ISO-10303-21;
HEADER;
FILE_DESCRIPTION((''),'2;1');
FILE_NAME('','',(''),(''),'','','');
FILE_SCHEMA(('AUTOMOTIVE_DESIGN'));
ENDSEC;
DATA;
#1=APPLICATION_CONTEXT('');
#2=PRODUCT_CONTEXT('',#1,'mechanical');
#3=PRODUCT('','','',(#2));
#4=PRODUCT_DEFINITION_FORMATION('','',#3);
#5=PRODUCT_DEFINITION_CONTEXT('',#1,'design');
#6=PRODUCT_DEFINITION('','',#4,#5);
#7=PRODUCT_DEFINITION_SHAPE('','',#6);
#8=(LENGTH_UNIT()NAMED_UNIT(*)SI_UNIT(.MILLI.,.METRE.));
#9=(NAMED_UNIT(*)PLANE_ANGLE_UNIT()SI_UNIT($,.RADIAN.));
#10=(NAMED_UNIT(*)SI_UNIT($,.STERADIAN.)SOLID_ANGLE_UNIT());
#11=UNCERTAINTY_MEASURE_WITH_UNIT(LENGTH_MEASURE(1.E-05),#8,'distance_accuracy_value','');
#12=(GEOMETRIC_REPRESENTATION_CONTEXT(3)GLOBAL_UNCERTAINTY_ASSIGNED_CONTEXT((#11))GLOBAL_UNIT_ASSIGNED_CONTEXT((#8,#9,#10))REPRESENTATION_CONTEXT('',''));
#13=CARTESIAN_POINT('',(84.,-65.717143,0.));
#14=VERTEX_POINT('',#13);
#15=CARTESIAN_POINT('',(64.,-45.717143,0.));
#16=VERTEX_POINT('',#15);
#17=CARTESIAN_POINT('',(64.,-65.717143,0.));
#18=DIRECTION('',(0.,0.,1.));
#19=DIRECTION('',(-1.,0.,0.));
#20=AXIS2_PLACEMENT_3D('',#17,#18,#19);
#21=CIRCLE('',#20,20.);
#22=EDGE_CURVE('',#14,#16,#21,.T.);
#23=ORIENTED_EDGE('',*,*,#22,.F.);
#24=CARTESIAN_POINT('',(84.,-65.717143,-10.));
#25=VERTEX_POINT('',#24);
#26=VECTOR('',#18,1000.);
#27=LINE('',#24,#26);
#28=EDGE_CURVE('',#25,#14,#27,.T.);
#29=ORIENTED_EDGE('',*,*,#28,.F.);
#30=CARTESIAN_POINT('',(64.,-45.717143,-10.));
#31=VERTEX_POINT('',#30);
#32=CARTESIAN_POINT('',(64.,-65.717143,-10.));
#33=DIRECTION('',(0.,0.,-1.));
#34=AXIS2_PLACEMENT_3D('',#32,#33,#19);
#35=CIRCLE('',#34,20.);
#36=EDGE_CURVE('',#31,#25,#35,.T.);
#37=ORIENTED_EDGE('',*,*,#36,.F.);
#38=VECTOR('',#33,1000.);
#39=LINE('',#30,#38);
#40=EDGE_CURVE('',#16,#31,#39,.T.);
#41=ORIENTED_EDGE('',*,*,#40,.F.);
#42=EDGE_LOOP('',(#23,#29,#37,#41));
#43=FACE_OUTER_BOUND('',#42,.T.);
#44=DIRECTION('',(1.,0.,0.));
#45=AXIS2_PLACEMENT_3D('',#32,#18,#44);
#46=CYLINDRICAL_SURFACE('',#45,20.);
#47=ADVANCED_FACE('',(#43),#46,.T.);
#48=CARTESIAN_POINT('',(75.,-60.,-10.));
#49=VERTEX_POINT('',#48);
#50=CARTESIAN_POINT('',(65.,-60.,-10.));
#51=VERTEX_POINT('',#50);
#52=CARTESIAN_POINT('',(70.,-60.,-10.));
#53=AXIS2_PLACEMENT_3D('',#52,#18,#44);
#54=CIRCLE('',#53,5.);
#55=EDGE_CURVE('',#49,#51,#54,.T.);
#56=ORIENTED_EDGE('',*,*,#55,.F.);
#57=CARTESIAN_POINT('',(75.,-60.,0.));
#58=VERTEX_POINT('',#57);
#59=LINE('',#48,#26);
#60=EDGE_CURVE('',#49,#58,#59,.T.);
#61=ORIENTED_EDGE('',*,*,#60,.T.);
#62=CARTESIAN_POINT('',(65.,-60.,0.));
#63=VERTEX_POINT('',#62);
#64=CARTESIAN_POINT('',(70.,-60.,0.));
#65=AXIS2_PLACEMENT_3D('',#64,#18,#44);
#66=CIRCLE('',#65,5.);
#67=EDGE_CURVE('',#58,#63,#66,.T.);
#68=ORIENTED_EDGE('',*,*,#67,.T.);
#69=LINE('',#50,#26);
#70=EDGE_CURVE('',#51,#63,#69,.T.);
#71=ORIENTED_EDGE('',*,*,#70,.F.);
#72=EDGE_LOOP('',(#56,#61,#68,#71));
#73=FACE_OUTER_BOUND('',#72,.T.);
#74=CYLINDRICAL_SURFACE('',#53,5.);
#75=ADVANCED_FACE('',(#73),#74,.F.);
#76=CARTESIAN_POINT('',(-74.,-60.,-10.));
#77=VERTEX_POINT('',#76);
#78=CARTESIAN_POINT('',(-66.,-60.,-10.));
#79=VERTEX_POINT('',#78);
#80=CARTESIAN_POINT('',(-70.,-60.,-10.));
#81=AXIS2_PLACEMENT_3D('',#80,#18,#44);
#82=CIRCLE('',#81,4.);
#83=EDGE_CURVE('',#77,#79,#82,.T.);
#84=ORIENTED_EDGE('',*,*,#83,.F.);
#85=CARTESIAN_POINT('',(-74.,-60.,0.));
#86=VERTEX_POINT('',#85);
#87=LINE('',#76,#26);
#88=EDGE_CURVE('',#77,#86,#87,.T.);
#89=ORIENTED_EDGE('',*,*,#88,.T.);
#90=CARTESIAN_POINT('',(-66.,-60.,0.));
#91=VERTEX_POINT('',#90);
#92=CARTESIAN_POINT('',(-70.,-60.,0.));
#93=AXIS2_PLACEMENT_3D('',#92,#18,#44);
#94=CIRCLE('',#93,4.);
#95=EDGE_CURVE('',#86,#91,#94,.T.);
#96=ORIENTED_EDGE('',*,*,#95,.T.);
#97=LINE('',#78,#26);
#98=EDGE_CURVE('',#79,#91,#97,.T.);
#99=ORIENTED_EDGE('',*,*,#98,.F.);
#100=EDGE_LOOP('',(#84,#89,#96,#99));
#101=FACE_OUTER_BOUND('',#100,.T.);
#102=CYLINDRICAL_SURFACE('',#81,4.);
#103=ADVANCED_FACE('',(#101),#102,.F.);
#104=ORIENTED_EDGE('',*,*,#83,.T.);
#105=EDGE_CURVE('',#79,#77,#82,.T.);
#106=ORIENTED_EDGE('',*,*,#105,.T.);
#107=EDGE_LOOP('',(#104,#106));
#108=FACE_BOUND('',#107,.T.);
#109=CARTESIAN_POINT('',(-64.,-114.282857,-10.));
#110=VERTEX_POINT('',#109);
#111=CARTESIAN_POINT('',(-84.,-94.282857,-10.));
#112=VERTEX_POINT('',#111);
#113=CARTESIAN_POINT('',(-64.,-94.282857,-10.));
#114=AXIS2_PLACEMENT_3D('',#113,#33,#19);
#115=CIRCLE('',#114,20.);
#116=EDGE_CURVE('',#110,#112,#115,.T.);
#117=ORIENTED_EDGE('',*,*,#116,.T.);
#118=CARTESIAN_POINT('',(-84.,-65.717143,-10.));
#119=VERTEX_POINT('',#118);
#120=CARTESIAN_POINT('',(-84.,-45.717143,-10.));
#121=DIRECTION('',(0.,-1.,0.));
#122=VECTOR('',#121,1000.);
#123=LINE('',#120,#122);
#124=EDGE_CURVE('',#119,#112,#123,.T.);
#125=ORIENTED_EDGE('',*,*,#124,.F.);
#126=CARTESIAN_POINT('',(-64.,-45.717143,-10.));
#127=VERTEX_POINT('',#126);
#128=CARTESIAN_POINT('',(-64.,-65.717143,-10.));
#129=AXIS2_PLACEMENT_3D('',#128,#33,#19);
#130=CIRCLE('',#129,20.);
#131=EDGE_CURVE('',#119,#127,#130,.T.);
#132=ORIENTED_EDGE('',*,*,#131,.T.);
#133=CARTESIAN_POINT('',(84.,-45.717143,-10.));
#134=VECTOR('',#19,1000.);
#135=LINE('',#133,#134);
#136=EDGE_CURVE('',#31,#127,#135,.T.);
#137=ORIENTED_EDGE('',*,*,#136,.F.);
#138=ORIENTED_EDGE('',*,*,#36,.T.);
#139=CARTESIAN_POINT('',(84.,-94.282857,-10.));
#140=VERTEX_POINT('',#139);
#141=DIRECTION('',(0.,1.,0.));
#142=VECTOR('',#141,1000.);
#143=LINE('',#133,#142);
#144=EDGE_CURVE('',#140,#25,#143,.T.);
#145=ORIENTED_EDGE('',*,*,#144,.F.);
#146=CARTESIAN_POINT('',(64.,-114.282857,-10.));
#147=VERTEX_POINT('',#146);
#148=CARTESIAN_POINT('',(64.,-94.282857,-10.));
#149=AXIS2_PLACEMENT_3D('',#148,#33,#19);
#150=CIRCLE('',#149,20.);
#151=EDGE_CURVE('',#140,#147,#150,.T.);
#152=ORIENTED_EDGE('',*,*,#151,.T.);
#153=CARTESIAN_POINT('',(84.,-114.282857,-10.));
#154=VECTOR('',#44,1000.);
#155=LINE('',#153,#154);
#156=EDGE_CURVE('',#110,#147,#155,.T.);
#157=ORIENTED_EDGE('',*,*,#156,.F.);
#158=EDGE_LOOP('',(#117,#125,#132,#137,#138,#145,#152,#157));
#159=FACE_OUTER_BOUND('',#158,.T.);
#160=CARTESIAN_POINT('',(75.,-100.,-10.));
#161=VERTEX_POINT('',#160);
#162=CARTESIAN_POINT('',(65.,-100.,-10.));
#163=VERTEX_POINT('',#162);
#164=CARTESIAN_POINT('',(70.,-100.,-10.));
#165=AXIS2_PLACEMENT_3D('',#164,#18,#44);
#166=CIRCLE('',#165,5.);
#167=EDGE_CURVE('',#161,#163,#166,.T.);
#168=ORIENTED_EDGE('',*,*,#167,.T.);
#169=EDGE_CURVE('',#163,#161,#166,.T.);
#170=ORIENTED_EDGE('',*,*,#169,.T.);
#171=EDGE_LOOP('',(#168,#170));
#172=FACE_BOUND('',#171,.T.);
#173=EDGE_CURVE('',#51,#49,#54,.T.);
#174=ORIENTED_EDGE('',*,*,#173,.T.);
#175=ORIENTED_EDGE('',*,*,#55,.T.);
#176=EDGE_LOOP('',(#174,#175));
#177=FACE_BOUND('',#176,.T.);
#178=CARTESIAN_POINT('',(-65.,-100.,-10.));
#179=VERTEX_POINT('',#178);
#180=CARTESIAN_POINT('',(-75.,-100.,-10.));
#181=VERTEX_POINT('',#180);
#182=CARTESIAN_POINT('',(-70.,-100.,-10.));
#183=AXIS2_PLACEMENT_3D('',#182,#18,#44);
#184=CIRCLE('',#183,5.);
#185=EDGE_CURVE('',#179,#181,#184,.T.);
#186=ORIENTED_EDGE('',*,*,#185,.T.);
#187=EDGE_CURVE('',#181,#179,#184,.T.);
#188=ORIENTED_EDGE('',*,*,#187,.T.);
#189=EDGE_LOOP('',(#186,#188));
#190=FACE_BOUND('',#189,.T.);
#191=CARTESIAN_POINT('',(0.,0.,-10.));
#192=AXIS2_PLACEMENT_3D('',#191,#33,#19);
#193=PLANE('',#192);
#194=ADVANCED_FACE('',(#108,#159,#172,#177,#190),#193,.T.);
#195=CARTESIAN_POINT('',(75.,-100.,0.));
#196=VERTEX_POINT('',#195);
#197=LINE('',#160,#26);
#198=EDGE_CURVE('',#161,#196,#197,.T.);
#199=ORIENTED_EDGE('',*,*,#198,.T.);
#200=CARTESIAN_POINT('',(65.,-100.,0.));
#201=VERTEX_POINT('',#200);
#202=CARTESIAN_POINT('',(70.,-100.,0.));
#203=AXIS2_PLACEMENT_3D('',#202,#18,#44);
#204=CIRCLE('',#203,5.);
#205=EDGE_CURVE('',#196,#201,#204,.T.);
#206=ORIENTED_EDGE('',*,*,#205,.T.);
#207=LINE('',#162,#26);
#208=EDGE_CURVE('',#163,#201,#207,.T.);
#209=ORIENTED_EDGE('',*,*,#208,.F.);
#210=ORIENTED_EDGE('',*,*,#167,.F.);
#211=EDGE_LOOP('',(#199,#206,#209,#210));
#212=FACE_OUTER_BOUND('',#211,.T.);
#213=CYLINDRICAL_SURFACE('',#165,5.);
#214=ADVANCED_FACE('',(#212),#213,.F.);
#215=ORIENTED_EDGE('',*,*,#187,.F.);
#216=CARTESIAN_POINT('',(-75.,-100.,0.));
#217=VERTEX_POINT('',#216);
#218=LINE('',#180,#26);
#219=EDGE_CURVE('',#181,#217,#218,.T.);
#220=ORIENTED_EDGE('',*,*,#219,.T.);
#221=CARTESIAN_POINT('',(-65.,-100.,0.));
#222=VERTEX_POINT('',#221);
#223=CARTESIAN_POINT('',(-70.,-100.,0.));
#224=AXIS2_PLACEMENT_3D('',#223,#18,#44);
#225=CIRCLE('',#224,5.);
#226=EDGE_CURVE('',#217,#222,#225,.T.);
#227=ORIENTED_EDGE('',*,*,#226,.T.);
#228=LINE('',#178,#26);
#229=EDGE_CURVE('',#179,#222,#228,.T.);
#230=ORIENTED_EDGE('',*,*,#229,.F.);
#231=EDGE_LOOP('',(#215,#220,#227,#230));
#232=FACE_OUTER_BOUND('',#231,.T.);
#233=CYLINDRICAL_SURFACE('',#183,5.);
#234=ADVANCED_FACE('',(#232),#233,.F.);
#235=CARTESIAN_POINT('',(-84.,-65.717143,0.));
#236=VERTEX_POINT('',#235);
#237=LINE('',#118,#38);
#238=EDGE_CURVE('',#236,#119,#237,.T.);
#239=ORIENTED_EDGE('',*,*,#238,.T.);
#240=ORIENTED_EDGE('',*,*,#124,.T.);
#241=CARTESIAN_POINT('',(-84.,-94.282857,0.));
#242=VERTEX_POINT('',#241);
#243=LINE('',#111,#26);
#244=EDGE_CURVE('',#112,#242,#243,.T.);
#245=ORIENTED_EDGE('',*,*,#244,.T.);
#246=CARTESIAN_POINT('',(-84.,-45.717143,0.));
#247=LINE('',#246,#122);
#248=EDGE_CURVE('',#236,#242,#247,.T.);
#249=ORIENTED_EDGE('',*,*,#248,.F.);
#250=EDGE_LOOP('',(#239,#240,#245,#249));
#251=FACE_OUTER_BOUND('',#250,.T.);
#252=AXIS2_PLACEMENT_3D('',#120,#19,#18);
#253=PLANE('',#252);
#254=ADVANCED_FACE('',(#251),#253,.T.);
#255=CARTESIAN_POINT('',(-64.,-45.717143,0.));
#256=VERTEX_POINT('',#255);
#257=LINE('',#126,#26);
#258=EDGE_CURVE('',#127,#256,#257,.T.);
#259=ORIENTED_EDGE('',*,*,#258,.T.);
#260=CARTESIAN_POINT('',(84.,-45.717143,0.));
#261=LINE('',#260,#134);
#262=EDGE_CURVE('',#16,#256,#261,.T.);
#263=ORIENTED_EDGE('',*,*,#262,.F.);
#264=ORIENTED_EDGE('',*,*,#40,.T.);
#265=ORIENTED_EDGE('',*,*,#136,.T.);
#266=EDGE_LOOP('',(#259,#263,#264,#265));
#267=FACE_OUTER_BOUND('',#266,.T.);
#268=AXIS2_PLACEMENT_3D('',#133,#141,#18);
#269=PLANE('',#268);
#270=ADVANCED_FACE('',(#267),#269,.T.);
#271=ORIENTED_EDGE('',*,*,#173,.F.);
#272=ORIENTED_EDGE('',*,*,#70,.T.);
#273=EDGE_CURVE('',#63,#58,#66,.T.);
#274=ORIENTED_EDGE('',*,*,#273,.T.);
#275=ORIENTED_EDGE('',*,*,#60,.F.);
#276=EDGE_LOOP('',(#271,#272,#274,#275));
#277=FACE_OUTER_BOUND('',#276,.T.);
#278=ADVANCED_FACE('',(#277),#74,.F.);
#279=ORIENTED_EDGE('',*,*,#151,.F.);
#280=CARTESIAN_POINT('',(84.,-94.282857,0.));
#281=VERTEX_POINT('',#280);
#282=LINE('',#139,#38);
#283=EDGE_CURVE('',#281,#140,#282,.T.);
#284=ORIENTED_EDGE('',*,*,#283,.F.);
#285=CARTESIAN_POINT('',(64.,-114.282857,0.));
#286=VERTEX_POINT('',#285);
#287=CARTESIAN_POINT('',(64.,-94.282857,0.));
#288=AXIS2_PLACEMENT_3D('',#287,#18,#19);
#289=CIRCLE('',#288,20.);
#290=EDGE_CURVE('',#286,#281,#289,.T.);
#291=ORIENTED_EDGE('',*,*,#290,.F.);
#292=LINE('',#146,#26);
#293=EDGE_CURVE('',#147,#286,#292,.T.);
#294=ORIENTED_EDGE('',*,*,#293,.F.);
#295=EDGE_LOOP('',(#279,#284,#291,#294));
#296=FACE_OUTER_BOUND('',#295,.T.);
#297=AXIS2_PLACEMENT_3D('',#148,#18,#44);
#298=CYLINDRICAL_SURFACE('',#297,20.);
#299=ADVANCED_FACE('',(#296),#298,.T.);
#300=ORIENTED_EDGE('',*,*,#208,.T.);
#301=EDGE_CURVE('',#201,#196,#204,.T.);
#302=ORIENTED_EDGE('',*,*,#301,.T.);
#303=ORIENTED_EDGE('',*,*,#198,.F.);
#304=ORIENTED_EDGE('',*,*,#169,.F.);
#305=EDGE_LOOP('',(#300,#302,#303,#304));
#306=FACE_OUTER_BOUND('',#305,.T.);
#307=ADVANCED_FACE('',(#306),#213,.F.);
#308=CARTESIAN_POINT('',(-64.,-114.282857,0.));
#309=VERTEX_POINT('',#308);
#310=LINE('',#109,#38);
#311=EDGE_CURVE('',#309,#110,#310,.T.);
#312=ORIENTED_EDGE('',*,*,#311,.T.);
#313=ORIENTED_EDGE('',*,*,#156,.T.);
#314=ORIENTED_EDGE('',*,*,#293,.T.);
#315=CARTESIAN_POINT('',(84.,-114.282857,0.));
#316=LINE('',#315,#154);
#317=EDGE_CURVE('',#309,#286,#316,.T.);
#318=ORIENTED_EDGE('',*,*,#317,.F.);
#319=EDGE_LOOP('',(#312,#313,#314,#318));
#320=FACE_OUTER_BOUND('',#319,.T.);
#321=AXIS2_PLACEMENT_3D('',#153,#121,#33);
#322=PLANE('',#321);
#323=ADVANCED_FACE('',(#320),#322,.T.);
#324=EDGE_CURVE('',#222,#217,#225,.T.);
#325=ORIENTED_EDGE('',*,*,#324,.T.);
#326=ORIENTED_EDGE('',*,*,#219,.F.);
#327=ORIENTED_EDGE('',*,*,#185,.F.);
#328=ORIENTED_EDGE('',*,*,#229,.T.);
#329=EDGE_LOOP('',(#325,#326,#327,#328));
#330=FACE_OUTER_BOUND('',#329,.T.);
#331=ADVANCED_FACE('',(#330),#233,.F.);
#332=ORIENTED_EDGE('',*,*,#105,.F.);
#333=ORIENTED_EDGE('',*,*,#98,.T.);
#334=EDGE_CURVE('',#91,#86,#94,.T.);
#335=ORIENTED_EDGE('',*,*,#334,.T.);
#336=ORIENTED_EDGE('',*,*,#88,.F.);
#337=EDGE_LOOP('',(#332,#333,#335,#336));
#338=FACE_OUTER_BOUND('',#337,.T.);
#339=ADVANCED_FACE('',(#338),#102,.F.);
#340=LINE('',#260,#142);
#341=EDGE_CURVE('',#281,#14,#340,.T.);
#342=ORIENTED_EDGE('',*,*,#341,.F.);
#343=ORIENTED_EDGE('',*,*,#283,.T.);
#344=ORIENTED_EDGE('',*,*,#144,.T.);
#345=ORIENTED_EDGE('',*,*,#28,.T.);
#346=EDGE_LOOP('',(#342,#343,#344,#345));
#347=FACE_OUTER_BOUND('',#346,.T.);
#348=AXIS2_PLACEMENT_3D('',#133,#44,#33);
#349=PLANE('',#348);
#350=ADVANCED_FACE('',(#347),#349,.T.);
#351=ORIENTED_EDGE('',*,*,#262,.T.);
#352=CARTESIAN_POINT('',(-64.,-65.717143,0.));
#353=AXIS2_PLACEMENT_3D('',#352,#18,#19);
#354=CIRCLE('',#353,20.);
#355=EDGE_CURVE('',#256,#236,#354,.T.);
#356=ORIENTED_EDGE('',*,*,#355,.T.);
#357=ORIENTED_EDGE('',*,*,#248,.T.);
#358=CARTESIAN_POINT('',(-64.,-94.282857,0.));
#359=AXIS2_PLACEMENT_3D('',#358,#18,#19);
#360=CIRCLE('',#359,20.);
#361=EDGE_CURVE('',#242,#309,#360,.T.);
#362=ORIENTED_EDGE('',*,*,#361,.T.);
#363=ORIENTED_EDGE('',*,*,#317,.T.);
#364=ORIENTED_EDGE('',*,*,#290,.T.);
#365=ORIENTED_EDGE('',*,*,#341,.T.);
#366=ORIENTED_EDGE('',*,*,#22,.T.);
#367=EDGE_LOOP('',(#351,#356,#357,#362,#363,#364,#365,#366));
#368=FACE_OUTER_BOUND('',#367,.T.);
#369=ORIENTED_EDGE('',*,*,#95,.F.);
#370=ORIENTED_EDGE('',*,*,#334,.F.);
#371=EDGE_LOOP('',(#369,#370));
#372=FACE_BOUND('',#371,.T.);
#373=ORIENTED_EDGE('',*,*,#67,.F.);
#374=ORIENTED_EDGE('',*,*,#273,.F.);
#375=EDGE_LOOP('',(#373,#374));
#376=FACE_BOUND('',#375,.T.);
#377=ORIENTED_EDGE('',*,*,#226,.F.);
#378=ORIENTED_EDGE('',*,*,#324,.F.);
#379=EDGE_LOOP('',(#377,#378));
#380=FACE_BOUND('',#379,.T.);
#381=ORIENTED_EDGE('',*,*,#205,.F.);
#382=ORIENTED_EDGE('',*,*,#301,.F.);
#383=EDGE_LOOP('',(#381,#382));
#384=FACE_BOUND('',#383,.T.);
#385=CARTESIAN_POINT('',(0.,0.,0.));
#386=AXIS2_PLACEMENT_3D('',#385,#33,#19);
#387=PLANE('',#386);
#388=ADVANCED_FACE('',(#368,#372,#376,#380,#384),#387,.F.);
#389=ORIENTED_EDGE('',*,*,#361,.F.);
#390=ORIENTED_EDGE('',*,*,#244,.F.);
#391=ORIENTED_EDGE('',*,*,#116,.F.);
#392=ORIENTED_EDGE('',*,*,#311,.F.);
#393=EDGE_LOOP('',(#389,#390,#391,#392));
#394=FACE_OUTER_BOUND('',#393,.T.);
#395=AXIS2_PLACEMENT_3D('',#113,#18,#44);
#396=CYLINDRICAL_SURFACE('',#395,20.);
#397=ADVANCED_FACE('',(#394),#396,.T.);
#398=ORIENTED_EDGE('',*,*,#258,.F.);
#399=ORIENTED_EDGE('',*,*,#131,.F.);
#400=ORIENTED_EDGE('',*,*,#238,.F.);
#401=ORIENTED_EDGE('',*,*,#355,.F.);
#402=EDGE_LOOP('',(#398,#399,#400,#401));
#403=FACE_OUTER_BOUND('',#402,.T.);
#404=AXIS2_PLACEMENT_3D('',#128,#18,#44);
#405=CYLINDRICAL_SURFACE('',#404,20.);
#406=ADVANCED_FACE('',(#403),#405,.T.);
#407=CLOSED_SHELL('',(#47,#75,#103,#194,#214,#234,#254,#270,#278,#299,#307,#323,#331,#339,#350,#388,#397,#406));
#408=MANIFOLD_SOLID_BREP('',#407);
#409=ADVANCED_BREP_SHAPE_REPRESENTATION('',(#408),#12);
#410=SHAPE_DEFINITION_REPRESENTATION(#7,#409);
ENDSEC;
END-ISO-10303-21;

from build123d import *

# Parameters (mm, degrees)
SKETCH_1_W          = 168
SKETCH_1_H          = 68.565713714
EXTRUDE_1_DEPTH     = 10
SKETCH_2_R          = 4
SKETCH_2_R_2        = 5
CUT_EXTRUDE_1_DEPTH = 10
FILLET_1_R          = 20


with BuildPart() as part:
    # 草图1 → 凸台-拉伸1 (new body)
    with BuildSketch(Plane.XY):
        with Locations((0, -80)):
            Rectangle(SKETCH_1_W, SKETCH_1_H)
    extrude(amount=-EXTRUDE_1_DEPTH)

    # 草图2 → 切除-拉伸1 (cut)
    with BuildSketch(Plane.XY):
        with Locations((-70, -60)):
            Circle(SKETCH_2_R)
        with Locations((-70, -100)):
            Circle(SKETCH_2_R_2)
        with Locations((70, -60)):
            Circle(SKETCH_2_R_2)
        with Locations((70, -100)):
            Circle(SKETCH_2_R_2)
    extrude(amount=-CUT_EXTRUDE_1_DEPTH, mode=Mode.SUBTRACT)

    # 圆角1
    fillet_1_edges = [part.edges().sort_by_distance(p)[0] for p in [
        (-84, -45.717143143, -5),
        (84, -45.717143143, -5),
        (84, -114.282856857, -5),
        (-84, -114.282856857, -5),
    ]]
    fillet(fillet_1_edges, radius=FILLET_1_R)


solid = part.part
